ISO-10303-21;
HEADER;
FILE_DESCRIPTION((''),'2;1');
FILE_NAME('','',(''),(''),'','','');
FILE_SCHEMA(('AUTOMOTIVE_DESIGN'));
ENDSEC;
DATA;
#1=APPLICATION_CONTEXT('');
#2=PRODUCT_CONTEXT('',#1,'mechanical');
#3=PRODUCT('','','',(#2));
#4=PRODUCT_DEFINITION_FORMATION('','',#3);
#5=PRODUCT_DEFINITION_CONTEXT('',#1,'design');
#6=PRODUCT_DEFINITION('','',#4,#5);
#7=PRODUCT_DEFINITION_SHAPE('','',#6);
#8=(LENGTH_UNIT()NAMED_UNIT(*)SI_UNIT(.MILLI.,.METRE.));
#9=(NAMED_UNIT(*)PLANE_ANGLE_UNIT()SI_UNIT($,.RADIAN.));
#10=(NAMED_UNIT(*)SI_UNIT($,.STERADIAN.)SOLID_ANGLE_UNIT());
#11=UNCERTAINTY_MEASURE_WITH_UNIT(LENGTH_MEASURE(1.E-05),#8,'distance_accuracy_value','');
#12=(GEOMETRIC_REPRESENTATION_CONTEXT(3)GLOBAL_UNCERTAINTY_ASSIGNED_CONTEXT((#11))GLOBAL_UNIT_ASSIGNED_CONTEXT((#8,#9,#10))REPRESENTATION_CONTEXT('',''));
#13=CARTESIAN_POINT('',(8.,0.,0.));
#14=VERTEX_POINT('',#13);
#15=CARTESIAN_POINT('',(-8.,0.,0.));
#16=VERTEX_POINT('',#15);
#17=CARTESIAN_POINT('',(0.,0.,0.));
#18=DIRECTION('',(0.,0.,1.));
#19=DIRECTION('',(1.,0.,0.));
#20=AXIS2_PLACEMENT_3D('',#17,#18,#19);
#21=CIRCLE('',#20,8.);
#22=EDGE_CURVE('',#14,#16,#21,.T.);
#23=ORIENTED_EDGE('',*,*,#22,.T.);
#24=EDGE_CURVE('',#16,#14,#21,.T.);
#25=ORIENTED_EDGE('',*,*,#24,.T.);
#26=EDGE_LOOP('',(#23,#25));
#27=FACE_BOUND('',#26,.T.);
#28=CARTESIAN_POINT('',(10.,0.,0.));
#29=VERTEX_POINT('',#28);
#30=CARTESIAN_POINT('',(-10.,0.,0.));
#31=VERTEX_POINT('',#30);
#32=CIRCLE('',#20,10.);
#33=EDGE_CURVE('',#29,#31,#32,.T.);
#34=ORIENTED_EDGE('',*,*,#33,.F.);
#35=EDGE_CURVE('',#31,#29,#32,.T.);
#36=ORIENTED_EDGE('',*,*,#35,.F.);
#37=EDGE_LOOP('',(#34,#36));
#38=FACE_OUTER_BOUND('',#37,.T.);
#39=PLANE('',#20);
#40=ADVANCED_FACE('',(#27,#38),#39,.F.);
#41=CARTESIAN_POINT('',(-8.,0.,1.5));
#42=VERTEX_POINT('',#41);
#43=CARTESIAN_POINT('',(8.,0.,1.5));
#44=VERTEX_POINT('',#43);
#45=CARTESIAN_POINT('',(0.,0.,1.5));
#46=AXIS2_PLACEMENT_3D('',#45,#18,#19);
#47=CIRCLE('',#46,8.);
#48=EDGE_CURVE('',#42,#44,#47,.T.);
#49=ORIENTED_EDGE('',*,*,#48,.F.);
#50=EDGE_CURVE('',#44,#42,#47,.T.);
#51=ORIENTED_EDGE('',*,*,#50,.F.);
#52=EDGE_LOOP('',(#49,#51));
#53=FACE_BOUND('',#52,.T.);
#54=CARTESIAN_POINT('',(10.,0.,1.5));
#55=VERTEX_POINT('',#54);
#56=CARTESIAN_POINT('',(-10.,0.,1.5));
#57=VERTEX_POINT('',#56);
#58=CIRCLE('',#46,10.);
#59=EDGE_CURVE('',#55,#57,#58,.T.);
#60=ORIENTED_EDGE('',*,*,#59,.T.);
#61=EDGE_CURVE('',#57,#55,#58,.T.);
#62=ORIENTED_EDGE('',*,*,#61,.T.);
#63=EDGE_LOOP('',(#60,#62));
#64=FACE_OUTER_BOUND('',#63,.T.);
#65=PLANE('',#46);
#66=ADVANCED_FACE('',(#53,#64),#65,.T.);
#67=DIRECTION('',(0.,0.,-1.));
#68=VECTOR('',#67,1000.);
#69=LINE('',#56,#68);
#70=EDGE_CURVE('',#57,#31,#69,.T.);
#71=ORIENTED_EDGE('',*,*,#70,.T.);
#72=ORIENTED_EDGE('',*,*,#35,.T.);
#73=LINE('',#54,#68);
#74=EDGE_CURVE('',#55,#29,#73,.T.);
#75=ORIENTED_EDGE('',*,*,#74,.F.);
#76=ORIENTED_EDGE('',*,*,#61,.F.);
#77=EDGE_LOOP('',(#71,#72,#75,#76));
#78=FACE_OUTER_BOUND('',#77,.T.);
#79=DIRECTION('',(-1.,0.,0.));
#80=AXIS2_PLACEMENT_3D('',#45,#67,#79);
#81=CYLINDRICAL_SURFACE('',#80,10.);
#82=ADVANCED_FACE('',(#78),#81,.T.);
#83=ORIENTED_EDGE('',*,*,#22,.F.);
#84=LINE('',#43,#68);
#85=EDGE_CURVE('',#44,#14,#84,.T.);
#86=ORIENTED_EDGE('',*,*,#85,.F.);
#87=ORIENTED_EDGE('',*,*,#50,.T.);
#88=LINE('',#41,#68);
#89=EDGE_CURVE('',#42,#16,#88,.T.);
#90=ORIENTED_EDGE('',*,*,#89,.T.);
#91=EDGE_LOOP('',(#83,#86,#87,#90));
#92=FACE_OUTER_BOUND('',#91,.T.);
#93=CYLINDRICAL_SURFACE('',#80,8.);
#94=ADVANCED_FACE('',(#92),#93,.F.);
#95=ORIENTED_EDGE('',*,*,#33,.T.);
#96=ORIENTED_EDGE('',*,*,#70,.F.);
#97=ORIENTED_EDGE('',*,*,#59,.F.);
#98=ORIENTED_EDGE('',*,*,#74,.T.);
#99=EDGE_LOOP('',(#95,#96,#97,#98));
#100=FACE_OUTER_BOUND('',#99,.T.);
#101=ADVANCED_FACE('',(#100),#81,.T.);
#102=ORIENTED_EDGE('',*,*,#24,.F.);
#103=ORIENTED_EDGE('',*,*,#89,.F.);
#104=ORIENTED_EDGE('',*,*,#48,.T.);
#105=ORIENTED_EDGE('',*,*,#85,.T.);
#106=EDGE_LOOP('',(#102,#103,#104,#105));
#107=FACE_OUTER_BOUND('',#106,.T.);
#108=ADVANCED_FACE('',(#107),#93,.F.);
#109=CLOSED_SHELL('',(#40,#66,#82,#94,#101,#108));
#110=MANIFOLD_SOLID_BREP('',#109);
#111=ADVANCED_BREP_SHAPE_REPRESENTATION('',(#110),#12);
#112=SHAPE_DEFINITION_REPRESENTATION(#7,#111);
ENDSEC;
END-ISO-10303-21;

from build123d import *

# Parameters (mm, degrees)
SKETCH_1_R      = 10
SKETCH_1_R_2    = 8
EXTRUDE_1_DEPTH = 1.5


with BuildPart() as part:
    # 草图1 → 凸台-拉伸1 (new body)
    with BuildSketch(Plane.XY):
        Circle(SKETCH_1_R)
        Circle(SKETCH_1_R_2, mode=Mode.SUBTRACT)
    extrude(amount=EXTRUDE_1_DEPTH)


solid = part.part
